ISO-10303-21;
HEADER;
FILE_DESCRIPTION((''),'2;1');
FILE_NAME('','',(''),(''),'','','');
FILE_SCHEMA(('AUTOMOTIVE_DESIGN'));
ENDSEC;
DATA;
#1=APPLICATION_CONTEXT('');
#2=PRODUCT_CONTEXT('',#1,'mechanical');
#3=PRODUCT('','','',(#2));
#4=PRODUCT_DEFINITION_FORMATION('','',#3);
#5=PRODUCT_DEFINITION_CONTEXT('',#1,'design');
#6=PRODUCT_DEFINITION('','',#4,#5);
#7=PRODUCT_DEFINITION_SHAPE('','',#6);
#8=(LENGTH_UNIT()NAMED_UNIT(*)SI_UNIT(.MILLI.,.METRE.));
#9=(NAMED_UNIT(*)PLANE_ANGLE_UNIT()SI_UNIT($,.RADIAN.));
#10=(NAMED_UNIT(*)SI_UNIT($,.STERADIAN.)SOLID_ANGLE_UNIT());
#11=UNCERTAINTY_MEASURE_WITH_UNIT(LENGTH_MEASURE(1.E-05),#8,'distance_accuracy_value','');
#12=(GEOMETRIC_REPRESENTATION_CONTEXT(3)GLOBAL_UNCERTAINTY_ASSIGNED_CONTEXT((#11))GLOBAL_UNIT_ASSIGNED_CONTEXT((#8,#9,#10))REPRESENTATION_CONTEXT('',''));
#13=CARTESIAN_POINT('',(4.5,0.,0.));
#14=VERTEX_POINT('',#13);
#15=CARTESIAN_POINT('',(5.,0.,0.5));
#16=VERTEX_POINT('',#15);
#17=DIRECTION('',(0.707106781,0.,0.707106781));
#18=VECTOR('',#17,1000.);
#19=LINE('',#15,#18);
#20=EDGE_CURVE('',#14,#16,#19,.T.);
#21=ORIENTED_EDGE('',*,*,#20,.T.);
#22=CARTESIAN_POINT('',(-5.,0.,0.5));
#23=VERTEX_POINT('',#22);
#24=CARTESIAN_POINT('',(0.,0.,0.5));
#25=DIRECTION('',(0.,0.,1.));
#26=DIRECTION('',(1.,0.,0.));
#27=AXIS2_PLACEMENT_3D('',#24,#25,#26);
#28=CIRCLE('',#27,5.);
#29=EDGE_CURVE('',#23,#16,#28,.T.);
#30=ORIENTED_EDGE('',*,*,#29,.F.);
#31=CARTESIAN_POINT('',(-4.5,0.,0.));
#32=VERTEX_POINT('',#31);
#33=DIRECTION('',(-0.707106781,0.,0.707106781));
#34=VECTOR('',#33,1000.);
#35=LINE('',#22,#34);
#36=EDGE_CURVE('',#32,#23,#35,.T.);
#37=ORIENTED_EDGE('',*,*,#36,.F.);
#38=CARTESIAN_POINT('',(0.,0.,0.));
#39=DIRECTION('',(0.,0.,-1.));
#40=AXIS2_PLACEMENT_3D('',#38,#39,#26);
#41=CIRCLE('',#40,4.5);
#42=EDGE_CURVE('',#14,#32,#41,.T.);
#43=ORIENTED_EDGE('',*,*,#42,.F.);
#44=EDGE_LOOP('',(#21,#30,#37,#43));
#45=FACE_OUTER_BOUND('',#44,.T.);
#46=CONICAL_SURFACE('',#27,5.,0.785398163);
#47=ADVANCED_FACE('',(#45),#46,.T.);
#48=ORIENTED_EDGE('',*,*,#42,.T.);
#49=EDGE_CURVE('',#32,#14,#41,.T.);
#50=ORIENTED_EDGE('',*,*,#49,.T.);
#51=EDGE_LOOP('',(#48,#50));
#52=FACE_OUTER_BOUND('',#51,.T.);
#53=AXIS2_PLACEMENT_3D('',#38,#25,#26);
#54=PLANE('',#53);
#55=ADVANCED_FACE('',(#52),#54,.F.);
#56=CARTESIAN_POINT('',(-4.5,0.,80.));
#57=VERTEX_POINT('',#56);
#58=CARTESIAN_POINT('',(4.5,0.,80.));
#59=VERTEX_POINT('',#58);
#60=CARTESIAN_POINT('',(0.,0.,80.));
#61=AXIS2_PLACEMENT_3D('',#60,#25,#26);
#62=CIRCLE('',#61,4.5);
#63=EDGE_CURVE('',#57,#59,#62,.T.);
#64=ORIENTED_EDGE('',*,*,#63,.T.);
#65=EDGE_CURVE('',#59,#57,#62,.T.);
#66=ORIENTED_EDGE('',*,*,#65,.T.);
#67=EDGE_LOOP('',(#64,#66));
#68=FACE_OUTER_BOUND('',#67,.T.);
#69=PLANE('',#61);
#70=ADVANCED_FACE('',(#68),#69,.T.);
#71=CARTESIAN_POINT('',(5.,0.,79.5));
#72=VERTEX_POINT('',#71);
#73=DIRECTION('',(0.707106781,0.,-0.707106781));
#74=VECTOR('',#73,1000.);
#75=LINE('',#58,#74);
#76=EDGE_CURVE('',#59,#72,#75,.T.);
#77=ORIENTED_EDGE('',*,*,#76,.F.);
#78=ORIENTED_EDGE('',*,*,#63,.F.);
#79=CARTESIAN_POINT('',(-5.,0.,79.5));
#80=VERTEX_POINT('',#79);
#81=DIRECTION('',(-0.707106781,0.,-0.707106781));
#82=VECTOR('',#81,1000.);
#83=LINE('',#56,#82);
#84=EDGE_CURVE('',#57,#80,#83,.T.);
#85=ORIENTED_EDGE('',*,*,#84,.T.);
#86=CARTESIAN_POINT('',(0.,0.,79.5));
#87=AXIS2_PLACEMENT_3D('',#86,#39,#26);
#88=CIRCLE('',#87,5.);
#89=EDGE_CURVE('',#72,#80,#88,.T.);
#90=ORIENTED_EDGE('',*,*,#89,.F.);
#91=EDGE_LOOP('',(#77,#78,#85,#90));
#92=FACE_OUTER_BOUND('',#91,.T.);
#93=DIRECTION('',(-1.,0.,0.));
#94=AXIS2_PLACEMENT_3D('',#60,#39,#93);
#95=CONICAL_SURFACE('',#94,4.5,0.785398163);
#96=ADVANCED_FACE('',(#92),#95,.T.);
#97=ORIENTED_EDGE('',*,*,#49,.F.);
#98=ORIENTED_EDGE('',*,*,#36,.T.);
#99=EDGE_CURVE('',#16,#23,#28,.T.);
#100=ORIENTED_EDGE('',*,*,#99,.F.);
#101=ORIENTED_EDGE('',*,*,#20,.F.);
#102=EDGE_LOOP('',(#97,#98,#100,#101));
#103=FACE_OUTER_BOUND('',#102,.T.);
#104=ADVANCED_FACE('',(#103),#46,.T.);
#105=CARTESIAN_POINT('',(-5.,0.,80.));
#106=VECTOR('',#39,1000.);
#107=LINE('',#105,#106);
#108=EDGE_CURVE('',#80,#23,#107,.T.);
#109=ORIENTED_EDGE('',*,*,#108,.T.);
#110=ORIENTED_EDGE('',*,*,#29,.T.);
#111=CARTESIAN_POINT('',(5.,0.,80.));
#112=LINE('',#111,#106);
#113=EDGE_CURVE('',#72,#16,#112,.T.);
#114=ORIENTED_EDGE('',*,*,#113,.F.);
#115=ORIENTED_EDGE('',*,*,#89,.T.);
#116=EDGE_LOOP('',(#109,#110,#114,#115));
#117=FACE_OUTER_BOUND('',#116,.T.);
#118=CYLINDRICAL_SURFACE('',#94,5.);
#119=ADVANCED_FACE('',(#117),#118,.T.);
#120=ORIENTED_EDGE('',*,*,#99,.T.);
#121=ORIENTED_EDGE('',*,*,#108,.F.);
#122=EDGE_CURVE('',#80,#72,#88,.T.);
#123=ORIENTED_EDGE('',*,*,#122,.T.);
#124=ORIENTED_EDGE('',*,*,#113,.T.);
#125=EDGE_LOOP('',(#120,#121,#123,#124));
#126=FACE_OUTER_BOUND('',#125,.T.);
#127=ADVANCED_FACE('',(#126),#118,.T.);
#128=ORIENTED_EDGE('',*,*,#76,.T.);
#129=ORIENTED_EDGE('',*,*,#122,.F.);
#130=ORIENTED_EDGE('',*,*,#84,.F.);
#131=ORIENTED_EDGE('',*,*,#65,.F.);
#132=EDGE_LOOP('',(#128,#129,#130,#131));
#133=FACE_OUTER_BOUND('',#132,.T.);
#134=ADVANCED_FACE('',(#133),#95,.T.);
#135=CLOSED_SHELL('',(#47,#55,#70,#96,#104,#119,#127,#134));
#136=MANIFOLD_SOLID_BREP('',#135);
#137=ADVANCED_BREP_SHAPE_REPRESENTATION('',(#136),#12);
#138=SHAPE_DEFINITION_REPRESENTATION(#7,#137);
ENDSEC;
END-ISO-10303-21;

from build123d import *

# Parameters (mm, degrees)
SKETCH_1_R      = 5
EXTRUDE_1_DEPTH = 80
CHAMFER_1_SIZE  = 0.5


with BuildPart() as part:
    # 草图1 → 凸台-拉伸1 (new body)
    with BuildSketch(Plane.XY):
        Circle(SKETCH_1_R)
    extrude(amount=EXTRUDE_1_DEPTH)

    # 倒角1
    chamfer_1_edges = [part.edges().sort_by_distance(p)[0] for p in [
        (-5, 0, 0),
        (-5, 0, 80),
    ]]
    chamfer(chamfer_1_edges, length=CHAMFER_1_SIZE)


solid = part.part
